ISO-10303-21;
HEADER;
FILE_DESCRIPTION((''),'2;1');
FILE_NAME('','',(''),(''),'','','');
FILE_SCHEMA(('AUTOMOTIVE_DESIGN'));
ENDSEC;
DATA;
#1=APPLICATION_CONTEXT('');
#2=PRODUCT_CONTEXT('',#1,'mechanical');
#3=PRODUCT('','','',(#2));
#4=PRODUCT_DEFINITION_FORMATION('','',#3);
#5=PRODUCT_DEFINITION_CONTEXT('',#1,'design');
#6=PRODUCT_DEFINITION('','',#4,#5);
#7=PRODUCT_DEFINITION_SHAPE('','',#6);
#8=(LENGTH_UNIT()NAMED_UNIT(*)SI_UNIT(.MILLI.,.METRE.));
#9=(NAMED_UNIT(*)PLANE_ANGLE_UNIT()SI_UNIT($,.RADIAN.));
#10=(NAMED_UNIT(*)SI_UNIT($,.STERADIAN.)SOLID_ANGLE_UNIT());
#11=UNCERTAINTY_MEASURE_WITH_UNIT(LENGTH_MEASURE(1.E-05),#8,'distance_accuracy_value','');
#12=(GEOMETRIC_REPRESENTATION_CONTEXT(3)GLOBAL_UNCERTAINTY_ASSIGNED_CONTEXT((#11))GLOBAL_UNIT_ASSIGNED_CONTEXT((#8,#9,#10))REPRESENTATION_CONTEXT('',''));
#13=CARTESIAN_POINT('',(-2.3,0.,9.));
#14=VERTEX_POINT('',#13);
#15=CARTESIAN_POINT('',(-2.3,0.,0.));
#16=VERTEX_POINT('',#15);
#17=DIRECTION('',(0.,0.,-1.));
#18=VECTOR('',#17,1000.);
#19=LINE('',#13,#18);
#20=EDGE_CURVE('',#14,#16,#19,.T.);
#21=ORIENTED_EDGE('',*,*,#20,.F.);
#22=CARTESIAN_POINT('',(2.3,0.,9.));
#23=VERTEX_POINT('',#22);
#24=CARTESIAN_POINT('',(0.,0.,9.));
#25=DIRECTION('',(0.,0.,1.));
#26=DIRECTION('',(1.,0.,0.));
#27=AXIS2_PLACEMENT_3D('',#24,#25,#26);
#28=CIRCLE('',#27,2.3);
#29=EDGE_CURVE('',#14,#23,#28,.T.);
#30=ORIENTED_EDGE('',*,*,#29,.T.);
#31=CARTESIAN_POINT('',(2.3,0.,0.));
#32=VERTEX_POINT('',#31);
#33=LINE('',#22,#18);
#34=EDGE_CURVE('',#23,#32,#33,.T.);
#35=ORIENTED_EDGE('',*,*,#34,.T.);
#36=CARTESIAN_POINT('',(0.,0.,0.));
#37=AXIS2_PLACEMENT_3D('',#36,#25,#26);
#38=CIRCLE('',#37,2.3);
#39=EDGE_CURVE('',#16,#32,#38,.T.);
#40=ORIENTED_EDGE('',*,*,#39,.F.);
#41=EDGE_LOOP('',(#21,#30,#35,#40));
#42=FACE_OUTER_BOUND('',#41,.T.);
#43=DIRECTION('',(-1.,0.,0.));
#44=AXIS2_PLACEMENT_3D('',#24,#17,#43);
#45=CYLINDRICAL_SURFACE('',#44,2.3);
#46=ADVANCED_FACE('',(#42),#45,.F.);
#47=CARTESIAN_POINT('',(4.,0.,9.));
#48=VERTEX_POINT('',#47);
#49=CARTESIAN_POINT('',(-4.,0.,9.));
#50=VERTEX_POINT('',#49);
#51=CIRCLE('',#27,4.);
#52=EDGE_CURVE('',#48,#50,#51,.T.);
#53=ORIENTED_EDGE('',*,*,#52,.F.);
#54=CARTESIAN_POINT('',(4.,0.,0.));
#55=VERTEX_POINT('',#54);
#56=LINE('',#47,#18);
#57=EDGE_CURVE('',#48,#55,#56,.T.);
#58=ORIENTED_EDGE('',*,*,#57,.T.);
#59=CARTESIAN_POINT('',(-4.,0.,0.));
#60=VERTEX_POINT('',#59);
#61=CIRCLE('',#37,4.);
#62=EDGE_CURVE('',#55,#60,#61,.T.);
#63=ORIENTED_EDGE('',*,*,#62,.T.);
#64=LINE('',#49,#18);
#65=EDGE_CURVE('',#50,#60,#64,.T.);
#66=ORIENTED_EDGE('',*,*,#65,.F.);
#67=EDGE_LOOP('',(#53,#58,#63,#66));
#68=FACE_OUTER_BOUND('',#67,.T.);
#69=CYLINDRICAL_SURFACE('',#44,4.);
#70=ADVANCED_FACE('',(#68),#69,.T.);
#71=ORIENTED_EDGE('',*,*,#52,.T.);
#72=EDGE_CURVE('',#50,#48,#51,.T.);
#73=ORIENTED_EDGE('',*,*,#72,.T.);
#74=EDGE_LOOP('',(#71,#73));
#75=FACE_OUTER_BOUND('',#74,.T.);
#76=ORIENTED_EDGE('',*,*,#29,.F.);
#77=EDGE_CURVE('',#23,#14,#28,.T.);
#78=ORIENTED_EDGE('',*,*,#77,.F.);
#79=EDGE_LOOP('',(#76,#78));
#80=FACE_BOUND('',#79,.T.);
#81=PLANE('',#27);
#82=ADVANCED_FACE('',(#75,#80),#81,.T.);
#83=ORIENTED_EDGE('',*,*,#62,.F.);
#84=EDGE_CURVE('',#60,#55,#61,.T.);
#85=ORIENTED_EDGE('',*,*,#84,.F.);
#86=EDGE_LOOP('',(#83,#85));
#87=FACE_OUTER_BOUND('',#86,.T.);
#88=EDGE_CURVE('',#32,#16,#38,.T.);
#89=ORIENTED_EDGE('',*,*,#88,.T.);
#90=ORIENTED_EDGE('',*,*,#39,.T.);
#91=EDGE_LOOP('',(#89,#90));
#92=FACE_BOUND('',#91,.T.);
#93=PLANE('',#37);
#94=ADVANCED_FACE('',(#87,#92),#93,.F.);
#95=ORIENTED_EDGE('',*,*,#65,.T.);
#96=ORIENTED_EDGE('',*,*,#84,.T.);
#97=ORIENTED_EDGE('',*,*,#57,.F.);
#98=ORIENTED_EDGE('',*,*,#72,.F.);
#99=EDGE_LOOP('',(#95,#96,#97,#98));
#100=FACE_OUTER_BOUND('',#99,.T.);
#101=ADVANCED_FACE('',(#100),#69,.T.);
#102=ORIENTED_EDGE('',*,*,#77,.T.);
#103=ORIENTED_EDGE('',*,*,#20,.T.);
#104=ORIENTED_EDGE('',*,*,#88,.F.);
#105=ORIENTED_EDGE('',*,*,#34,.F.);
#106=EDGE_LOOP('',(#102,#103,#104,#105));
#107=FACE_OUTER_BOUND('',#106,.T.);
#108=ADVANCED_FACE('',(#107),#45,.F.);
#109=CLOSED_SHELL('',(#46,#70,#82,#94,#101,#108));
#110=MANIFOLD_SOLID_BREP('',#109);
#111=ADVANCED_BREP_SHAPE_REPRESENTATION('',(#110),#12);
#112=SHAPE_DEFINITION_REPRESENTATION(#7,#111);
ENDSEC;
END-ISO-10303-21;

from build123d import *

# Parameters (mm, degrees)
SKETCH1_R           = 4
SKETCH1_R_2         = 2.3
BOSS_EXTRUDE1_DEPTH = 9


with BuildPart() as part:
    # Sketch1 → Boss-Extrude1 (new body)
    with BuildSketch(Plane.XY):
        Circle(SKETCH1_R)
        Circle(SKETCH1_R_2, mode=Mode.SUBTRACT)
    extrude(amount=BOSS_EXTRUDE1_DEPTH)


solid = part.part
